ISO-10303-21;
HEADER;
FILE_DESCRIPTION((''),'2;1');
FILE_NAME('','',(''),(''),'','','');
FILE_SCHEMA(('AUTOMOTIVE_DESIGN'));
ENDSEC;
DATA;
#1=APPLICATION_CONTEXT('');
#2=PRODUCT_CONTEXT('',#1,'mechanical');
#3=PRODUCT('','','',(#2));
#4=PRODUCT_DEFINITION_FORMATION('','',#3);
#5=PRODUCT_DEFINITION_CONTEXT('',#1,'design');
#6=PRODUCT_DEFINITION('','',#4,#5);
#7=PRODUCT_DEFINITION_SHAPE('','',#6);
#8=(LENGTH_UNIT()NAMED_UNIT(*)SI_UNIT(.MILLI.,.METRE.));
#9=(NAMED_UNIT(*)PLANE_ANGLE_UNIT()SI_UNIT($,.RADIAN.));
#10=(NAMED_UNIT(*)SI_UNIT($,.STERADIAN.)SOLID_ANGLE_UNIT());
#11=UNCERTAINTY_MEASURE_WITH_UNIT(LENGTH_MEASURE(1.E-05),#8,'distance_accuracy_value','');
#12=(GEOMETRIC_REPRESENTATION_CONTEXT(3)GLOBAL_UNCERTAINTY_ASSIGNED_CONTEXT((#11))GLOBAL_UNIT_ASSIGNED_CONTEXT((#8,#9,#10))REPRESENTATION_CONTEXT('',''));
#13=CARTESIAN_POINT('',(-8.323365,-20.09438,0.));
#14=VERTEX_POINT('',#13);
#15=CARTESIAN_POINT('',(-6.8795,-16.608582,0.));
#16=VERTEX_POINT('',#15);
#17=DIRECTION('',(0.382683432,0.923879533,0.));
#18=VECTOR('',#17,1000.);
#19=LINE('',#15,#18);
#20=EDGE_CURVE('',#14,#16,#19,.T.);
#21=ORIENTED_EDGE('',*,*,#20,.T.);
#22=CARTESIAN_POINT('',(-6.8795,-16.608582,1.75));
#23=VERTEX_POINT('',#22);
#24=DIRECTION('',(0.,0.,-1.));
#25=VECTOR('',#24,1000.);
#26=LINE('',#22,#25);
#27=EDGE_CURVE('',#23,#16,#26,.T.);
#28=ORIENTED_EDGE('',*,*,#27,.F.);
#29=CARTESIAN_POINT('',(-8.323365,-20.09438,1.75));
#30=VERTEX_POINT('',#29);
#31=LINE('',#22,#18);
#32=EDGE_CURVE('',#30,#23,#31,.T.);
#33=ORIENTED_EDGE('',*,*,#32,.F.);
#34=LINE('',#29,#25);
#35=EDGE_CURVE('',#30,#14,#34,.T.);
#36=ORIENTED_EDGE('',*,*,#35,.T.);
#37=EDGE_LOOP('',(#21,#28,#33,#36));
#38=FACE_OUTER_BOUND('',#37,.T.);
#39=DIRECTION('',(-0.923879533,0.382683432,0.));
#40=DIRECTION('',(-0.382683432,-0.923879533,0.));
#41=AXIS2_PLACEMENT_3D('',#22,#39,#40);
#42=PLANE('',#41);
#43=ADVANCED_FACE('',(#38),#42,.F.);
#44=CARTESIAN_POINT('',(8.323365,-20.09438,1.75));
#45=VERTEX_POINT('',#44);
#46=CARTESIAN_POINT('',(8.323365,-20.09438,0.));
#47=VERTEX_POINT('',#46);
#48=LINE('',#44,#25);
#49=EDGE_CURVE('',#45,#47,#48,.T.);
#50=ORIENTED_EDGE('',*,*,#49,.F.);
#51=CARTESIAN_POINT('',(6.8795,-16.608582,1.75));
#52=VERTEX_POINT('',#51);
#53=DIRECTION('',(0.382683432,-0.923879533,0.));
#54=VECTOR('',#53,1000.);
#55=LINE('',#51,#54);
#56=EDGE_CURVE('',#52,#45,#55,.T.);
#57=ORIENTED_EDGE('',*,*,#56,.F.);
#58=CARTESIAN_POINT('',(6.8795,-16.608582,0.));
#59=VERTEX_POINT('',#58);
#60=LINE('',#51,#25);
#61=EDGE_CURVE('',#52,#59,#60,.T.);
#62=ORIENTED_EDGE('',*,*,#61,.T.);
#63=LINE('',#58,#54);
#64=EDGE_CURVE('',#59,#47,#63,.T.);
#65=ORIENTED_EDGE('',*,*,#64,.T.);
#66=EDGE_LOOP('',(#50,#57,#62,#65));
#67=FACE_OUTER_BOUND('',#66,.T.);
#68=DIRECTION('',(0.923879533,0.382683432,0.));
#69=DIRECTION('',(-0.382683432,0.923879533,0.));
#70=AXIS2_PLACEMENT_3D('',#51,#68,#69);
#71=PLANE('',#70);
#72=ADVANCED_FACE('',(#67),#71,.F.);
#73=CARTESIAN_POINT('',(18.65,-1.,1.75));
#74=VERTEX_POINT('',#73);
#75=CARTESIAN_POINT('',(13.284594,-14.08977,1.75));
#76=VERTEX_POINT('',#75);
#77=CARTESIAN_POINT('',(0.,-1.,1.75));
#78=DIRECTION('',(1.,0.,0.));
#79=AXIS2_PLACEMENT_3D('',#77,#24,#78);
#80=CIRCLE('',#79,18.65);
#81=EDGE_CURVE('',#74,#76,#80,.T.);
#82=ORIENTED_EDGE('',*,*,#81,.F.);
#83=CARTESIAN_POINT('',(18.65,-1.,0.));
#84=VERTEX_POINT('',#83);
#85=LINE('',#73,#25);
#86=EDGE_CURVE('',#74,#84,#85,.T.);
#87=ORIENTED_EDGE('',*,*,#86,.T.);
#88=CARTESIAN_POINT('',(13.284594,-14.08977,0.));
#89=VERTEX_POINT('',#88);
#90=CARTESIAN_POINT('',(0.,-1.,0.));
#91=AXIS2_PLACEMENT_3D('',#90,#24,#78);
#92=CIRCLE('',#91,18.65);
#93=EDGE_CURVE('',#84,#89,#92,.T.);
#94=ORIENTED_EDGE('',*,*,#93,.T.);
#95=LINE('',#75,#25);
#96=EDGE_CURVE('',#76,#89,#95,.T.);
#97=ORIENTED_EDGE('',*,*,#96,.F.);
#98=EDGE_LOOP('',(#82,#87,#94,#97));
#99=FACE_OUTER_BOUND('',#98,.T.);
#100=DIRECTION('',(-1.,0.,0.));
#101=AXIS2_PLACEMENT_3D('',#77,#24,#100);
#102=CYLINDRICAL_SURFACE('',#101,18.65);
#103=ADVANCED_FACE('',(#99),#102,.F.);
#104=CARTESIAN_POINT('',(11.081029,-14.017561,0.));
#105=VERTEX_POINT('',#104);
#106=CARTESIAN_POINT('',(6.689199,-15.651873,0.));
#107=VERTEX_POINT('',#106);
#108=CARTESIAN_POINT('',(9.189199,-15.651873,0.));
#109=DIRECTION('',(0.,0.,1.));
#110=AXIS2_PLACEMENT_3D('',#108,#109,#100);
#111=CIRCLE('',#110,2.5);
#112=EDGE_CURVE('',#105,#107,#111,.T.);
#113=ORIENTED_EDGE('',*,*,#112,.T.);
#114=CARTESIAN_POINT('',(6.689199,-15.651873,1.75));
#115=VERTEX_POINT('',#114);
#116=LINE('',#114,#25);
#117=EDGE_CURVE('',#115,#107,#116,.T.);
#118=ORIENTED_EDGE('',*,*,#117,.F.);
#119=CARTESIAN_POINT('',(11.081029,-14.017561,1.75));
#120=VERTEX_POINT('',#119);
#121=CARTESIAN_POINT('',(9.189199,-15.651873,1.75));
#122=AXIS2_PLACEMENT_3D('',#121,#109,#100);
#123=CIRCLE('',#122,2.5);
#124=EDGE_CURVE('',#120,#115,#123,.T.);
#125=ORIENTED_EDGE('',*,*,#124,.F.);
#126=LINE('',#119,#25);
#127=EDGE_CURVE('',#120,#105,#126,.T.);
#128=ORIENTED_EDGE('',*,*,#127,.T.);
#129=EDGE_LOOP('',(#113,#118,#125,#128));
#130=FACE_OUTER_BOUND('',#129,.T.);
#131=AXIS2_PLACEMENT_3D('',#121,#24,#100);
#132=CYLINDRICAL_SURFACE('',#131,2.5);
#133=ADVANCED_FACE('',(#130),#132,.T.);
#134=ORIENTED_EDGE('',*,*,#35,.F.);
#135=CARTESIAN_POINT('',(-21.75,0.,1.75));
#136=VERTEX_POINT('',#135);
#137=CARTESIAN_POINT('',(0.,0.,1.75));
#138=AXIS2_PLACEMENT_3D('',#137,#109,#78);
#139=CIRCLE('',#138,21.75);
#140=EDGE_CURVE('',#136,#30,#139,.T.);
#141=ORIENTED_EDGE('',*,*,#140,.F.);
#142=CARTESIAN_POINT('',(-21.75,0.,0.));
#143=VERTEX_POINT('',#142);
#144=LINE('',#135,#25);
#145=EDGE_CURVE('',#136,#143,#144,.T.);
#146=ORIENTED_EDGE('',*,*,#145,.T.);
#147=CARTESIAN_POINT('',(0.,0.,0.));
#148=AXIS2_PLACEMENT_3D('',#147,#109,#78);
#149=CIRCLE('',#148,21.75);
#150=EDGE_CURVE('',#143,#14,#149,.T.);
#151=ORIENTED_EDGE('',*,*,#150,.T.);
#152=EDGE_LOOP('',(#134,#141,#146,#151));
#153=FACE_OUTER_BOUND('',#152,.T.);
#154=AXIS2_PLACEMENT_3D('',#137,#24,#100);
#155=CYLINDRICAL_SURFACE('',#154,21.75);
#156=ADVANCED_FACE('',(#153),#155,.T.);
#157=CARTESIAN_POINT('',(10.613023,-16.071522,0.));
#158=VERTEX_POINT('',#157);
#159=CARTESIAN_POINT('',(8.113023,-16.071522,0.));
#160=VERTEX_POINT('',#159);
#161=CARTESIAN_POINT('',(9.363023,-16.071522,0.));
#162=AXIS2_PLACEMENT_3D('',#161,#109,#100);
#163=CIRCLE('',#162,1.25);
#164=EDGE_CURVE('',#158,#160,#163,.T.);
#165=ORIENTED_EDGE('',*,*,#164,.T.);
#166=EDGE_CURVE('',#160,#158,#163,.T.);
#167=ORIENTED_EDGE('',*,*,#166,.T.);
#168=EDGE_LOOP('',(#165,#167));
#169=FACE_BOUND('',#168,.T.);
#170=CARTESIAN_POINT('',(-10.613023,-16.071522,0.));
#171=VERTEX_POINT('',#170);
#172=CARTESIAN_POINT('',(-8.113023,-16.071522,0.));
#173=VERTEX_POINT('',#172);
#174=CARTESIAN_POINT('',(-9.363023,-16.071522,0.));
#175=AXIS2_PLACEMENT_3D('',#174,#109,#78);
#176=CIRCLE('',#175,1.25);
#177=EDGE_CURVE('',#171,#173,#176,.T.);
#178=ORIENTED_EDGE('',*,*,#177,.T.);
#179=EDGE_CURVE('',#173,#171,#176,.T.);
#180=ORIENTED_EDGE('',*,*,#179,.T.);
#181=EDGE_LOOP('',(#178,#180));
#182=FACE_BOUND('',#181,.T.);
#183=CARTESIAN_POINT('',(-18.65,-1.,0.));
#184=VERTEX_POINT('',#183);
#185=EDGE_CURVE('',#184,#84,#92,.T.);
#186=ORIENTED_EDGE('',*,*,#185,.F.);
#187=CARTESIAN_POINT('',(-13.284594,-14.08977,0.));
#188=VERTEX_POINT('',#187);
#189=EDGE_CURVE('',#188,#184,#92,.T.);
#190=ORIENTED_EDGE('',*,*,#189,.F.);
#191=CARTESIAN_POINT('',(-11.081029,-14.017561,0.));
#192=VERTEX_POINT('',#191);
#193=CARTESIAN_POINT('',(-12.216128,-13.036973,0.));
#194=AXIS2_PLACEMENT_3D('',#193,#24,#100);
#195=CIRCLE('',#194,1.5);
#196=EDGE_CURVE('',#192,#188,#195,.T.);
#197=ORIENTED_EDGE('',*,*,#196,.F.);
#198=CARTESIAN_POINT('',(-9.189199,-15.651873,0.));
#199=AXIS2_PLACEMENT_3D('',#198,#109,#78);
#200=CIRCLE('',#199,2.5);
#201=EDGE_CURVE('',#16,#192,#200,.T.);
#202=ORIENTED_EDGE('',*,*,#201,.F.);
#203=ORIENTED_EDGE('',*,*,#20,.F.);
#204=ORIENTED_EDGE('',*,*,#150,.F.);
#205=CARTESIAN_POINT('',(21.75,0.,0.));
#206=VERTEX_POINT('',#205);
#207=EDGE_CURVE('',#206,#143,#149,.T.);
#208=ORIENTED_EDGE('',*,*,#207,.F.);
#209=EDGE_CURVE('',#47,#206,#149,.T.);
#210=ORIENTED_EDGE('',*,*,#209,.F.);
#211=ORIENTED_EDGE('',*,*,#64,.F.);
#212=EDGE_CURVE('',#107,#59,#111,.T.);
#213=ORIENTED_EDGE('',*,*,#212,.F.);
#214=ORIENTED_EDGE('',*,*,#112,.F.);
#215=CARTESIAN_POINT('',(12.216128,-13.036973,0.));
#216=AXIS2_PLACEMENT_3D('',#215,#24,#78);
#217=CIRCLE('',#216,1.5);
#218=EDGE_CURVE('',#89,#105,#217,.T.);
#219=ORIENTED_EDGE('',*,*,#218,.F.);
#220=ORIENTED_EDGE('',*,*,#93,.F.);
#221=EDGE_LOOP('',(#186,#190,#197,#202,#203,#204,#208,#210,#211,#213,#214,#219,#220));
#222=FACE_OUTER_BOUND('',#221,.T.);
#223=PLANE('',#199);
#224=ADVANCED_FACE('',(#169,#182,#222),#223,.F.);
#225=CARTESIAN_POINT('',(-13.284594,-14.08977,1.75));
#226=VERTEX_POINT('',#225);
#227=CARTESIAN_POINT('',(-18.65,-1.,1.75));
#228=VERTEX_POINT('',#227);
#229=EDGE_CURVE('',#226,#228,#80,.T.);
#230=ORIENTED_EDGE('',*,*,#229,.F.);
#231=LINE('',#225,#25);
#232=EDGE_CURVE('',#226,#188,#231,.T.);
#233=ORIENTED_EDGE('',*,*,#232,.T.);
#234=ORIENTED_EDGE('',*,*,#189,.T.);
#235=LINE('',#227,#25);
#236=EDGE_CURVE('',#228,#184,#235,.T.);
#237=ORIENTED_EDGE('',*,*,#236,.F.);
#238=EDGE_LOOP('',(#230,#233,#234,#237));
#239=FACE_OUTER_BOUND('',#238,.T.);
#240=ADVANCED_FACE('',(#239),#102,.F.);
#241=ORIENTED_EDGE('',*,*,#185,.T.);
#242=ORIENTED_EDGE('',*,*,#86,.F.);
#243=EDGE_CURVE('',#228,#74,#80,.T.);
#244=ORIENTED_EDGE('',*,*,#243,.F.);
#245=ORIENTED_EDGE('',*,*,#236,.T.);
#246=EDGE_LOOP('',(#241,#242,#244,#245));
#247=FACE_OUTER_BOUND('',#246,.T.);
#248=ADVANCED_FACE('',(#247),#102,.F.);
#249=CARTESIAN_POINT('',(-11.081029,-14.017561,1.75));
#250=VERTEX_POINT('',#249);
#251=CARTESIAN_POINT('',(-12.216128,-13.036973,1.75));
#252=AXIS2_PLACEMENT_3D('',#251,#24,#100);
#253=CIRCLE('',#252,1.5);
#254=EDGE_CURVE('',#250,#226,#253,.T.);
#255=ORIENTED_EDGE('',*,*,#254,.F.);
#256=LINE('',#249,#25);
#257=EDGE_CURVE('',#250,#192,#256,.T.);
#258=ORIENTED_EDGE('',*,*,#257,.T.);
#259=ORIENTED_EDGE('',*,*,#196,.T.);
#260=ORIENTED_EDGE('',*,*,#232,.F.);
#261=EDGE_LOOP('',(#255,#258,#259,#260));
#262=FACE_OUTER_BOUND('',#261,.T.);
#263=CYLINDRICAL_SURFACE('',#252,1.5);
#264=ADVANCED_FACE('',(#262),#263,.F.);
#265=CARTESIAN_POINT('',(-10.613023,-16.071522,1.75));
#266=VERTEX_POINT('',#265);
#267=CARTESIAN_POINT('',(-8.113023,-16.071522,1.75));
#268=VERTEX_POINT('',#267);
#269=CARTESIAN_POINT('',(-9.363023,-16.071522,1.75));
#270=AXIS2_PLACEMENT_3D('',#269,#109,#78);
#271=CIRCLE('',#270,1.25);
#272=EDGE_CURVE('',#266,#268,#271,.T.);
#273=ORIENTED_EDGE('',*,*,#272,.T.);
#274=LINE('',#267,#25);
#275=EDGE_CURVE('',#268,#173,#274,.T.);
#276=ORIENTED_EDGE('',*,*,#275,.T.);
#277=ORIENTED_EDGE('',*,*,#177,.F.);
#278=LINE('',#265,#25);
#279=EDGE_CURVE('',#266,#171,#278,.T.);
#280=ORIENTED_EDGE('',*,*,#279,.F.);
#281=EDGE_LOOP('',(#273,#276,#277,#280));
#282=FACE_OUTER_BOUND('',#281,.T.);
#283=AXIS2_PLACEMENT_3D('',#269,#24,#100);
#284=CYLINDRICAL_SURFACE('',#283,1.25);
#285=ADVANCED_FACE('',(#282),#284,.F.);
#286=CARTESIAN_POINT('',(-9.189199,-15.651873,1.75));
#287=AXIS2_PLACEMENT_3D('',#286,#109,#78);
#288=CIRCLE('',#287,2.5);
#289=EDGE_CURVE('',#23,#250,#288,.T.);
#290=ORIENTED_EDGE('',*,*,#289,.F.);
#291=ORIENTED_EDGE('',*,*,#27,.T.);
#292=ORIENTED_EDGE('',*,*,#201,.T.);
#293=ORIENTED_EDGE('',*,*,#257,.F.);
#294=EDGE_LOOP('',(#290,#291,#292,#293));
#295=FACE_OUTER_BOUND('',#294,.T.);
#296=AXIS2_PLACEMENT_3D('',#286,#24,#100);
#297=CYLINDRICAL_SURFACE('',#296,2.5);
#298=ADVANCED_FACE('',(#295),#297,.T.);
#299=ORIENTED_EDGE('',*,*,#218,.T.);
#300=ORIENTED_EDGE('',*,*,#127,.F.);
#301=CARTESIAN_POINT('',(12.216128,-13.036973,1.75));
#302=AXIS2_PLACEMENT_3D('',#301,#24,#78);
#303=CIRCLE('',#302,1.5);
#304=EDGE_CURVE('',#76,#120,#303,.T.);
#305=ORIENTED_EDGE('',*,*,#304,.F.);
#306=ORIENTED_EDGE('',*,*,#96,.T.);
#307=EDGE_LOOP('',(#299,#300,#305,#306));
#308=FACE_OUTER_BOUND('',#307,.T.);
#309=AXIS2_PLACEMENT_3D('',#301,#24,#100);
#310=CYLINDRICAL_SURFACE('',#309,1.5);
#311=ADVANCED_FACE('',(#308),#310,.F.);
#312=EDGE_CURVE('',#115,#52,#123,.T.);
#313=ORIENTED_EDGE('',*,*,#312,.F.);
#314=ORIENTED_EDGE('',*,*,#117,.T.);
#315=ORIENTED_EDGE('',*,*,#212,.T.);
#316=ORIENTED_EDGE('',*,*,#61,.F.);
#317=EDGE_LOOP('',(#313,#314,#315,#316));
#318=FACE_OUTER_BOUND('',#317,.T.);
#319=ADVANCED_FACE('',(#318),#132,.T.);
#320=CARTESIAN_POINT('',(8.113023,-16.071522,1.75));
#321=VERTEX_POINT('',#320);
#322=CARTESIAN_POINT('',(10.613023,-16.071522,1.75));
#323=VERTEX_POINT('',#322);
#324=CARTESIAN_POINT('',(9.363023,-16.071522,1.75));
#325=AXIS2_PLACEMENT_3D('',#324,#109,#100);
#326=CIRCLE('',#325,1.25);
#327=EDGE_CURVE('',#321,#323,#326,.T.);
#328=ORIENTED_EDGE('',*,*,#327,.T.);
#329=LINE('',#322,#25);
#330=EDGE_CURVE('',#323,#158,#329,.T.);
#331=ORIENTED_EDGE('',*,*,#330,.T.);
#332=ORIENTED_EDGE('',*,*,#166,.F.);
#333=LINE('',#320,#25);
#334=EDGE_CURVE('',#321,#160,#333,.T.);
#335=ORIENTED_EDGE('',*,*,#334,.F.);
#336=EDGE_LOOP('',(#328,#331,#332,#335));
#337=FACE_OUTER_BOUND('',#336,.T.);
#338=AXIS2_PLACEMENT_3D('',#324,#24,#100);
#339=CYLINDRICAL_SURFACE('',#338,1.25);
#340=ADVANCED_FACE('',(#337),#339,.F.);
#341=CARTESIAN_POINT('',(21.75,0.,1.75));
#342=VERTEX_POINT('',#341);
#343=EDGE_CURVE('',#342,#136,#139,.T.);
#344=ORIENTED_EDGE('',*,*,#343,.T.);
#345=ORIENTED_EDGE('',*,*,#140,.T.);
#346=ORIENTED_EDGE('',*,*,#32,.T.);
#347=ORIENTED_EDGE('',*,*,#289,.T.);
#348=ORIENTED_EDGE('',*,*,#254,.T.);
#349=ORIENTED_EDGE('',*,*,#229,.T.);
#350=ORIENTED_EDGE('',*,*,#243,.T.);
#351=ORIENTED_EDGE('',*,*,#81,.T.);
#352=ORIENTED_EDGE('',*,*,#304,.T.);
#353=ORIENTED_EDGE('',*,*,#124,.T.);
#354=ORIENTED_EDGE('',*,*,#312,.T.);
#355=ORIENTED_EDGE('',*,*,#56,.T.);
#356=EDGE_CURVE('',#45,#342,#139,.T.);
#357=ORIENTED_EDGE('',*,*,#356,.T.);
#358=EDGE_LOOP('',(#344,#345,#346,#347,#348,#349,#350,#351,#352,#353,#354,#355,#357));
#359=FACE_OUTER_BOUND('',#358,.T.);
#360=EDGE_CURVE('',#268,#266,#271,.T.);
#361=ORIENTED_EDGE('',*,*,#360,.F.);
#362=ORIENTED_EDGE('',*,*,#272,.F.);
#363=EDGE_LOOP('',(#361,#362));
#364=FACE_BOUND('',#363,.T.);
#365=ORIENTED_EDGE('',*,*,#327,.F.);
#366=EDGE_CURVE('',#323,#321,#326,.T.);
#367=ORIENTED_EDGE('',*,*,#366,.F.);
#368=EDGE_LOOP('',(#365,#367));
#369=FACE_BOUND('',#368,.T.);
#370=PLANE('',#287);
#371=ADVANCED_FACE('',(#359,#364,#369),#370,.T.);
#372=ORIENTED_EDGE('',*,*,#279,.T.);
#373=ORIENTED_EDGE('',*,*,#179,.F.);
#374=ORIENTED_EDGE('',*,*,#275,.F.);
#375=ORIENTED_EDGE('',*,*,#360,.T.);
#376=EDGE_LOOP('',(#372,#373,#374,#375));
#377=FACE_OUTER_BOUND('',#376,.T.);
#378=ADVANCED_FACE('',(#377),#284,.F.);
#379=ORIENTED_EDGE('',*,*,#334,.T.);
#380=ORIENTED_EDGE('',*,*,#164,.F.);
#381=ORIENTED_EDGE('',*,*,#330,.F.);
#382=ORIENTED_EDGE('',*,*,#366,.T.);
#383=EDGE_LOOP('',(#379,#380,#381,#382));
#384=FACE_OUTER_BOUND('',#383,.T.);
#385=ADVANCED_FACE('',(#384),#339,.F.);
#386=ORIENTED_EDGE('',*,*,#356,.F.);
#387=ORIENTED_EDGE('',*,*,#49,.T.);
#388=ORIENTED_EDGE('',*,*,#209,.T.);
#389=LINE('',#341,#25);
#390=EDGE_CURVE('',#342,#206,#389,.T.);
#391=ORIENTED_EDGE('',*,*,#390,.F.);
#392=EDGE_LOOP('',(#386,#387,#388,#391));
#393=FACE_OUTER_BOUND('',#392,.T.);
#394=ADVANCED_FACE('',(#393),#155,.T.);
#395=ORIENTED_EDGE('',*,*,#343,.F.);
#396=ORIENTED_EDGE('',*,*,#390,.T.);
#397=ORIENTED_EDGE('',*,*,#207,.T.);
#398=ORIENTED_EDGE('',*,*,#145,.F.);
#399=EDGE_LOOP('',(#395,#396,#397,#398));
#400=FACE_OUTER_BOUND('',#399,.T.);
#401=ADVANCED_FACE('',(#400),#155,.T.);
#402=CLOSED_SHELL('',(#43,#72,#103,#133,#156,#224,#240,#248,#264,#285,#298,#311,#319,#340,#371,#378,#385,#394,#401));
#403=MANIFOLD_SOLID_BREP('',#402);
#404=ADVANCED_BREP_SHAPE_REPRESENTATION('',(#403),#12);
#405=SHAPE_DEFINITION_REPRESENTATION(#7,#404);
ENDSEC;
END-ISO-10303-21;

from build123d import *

# Parameters (mm, degrees)
SKETCH1_R          = 1.25
BASE_EXTRUDE_DEPTH = 1.75


with BuildPart() as part:
    # Sketch1 → Base-Extrude (new body)
    with BuildSketch(Plane.XY):
        with BuildLine():
            Line((-6.879499755, -16.608581611), (-8.323364654, -20.094379832))
            ThreePointArc((-8.323364654, -20.094379832), (0, 21.75), (8.323364654, -20.094379832))
            Line((8.323364654, -20.094379832), (6.879499755, -16.608581611))
            ThreePointArc((6.879499755, -16.608581611), (7.876948304, -13.523963446), (11.081029231, -14.017560694))
            ThreePointArc((11.081029231, -14.017560694), (12.16700015, -14.536168573), (13.28459359, -14.08976979))
            ThreePointArc((13.28459359, -14.08976979), (0, 17.65), (-13.28459359, -14.08976979))
            ThreePointArc((-13.28459359, -14.08976979), (-12.16700015, -14.536168573), (-11.081029231, -14.017560694))
            ThreePointArc((-11.081029231, -14.017560694), (-7.876948304, -13.523963446), (-6.879499755, -16.608581611))
        make_face()
        with Locations((-9.363022706, -16.071521577)):
            Circle(SKETCH1_R, mode=Mode.SUBTRACT)
        with Locations(Location((9.363022706, -16.071521577, 0), (0, 0, 180))):
            Circle(SKETCH1_R, mode=Mode.SUBTRACT)
    extrude(amount=BASE_EXTRUDE_DEPTH)


solid = part.part
